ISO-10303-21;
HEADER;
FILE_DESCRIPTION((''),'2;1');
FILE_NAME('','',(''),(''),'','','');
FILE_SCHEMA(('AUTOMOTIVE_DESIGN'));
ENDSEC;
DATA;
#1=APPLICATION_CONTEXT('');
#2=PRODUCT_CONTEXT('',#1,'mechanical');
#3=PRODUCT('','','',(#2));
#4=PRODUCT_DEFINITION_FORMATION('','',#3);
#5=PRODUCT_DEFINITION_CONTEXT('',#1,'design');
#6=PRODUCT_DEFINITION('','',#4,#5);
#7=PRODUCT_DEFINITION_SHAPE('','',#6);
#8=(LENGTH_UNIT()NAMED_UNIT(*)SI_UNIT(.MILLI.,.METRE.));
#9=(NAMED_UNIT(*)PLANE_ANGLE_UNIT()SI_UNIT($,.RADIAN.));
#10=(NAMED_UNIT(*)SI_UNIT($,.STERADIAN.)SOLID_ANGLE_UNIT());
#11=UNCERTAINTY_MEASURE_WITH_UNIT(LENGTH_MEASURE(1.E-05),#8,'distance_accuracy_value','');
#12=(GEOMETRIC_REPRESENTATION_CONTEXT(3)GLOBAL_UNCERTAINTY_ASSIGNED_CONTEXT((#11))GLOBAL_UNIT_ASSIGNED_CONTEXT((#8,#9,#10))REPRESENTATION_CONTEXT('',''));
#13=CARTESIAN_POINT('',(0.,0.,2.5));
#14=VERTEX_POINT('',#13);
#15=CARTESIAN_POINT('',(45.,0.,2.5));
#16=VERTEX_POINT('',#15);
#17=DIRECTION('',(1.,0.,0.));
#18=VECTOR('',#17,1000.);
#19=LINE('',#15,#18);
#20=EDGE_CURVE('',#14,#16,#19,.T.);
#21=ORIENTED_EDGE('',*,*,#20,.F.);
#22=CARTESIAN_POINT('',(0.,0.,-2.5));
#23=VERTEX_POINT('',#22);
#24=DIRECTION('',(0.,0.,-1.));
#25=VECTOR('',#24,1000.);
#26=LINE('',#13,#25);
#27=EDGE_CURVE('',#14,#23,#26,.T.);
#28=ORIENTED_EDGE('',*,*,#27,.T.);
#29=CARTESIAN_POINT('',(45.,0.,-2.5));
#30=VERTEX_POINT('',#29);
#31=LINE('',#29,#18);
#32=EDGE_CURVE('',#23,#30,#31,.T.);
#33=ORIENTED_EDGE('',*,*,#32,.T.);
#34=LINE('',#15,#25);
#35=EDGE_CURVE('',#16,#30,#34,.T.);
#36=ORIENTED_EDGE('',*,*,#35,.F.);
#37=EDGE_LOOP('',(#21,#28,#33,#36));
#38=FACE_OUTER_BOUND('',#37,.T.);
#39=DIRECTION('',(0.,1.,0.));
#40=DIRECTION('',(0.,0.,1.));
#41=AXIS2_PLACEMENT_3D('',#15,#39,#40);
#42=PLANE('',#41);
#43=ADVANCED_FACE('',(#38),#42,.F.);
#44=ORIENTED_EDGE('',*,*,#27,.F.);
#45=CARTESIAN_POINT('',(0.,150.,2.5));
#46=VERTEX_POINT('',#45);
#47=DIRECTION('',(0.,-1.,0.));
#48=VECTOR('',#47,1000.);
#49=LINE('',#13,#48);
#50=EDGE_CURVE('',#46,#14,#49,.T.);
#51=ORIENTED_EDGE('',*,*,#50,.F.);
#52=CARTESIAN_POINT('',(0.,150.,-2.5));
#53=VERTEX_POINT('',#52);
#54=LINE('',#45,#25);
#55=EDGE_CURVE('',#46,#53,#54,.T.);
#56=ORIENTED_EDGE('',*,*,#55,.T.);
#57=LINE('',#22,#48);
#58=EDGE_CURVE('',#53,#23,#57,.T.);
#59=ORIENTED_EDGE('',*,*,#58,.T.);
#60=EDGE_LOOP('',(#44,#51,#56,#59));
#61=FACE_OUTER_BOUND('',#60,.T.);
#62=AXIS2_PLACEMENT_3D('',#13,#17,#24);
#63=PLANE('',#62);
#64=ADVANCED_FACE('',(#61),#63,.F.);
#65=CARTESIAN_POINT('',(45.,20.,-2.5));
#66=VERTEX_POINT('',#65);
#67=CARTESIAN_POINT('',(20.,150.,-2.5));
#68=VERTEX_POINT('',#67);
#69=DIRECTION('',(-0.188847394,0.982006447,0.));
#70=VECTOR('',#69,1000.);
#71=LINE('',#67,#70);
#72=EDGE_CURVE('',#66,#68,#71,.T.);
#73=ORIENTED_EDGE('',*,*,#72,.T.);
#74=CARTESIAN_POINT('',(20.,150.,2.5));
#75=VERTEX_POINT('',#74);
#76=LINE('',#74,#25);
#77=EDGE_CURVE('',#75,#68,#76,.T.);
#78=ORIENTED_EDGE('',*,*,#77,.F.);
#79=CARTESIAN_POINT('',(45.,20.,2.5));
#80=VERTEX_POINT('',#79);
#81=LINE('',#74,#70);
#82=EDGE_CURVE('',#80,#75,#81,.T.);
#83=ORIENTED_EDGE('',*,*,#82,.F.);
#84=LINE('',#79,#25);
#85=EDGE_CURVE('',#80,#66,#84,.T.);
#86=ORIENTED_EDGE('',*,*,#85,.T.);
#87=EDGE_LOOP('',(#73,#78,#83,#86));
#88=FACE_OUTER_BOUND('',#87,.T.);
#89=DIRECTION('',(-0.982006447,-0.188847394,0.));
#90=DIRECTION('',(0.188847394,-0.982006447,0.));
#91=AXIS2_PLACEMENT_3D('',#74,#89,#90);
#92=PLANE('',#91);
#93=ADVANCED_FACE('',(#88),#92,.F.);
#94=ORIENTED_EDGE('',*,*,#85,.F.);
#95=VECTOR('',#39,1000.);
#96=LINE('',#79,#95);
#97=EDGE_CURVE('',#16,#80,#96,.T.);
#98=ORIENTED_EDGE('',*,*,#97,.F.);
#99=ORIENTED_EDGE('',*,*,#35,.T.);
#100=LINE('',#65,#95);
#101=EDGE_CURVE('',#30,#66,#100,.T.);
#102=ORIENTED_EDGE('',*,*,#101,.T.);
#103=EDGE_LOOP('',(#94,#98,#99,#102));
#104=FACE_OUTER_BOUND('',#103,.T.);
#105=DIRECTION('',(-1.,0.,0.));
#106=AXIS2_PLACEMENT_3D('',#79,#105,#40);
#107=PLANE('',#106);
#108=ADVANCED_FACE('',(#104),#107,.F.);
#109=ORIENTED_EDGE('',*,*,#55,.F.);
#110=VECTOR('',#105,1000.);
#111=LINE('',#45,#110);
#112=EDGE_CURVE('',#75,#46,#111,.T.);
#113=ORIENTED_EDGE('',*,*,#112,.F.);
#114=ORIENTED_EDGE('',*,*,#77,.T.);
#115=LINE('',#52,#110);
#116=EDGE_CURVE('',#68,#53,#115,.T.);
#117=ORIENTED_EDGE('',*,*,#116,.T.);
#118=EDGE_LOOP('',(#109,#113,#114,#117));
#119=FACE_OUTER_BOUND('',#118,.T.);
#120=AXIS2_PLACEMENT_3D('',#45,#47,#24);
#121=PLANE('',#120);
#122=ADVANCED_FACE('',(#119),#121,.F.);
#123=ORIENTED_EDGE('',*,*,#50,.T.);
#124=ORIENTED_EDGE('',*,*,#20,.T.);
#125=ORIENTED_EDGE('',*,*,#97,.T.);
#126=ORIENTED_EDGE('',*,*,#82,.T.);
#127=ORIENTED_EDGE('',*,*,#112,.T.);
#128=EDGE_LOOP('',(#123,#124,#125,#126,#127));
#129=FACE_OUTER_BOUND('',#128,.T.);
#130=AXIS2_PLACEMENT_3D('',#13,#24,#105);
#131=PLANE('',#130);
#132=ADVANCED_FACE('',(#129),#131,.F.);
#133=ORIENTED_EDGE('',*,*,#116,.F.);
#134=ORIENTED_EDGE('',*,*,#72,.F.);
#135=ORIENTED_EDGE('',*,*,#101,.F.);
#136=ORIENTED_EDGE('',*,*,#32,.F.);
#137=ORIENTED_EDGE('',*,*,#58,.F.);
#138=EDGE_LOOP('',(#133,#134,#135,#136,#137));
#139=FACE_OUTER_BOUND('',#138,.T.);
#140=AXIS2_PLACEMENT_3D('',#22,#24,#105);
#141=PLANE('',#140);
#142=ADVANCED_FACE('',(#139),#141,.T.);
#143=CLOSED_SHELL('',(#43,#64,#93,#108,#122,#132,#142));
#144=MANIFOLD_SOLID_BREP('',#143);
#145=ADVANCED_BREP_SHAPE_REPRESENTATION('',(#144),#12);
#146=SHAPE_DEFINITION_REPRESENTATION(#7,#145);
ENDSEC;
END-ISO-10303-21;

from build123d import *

# Parameters (mm, degrees)
EXTRUDE_1_DEPTH = 2.5


with BuildPart() as part:
    # 草图1 → 凸台-拉伸1 (new, symmetric)
    with BuildSketch(Plane.XY):
        Polygon((0, 0), (0, 150), (20, 150), (45, 20), (45, 0), align=None)
    extrude(amount=EXTRUDE_1_DEPTH, both=True)


solid = part.part
